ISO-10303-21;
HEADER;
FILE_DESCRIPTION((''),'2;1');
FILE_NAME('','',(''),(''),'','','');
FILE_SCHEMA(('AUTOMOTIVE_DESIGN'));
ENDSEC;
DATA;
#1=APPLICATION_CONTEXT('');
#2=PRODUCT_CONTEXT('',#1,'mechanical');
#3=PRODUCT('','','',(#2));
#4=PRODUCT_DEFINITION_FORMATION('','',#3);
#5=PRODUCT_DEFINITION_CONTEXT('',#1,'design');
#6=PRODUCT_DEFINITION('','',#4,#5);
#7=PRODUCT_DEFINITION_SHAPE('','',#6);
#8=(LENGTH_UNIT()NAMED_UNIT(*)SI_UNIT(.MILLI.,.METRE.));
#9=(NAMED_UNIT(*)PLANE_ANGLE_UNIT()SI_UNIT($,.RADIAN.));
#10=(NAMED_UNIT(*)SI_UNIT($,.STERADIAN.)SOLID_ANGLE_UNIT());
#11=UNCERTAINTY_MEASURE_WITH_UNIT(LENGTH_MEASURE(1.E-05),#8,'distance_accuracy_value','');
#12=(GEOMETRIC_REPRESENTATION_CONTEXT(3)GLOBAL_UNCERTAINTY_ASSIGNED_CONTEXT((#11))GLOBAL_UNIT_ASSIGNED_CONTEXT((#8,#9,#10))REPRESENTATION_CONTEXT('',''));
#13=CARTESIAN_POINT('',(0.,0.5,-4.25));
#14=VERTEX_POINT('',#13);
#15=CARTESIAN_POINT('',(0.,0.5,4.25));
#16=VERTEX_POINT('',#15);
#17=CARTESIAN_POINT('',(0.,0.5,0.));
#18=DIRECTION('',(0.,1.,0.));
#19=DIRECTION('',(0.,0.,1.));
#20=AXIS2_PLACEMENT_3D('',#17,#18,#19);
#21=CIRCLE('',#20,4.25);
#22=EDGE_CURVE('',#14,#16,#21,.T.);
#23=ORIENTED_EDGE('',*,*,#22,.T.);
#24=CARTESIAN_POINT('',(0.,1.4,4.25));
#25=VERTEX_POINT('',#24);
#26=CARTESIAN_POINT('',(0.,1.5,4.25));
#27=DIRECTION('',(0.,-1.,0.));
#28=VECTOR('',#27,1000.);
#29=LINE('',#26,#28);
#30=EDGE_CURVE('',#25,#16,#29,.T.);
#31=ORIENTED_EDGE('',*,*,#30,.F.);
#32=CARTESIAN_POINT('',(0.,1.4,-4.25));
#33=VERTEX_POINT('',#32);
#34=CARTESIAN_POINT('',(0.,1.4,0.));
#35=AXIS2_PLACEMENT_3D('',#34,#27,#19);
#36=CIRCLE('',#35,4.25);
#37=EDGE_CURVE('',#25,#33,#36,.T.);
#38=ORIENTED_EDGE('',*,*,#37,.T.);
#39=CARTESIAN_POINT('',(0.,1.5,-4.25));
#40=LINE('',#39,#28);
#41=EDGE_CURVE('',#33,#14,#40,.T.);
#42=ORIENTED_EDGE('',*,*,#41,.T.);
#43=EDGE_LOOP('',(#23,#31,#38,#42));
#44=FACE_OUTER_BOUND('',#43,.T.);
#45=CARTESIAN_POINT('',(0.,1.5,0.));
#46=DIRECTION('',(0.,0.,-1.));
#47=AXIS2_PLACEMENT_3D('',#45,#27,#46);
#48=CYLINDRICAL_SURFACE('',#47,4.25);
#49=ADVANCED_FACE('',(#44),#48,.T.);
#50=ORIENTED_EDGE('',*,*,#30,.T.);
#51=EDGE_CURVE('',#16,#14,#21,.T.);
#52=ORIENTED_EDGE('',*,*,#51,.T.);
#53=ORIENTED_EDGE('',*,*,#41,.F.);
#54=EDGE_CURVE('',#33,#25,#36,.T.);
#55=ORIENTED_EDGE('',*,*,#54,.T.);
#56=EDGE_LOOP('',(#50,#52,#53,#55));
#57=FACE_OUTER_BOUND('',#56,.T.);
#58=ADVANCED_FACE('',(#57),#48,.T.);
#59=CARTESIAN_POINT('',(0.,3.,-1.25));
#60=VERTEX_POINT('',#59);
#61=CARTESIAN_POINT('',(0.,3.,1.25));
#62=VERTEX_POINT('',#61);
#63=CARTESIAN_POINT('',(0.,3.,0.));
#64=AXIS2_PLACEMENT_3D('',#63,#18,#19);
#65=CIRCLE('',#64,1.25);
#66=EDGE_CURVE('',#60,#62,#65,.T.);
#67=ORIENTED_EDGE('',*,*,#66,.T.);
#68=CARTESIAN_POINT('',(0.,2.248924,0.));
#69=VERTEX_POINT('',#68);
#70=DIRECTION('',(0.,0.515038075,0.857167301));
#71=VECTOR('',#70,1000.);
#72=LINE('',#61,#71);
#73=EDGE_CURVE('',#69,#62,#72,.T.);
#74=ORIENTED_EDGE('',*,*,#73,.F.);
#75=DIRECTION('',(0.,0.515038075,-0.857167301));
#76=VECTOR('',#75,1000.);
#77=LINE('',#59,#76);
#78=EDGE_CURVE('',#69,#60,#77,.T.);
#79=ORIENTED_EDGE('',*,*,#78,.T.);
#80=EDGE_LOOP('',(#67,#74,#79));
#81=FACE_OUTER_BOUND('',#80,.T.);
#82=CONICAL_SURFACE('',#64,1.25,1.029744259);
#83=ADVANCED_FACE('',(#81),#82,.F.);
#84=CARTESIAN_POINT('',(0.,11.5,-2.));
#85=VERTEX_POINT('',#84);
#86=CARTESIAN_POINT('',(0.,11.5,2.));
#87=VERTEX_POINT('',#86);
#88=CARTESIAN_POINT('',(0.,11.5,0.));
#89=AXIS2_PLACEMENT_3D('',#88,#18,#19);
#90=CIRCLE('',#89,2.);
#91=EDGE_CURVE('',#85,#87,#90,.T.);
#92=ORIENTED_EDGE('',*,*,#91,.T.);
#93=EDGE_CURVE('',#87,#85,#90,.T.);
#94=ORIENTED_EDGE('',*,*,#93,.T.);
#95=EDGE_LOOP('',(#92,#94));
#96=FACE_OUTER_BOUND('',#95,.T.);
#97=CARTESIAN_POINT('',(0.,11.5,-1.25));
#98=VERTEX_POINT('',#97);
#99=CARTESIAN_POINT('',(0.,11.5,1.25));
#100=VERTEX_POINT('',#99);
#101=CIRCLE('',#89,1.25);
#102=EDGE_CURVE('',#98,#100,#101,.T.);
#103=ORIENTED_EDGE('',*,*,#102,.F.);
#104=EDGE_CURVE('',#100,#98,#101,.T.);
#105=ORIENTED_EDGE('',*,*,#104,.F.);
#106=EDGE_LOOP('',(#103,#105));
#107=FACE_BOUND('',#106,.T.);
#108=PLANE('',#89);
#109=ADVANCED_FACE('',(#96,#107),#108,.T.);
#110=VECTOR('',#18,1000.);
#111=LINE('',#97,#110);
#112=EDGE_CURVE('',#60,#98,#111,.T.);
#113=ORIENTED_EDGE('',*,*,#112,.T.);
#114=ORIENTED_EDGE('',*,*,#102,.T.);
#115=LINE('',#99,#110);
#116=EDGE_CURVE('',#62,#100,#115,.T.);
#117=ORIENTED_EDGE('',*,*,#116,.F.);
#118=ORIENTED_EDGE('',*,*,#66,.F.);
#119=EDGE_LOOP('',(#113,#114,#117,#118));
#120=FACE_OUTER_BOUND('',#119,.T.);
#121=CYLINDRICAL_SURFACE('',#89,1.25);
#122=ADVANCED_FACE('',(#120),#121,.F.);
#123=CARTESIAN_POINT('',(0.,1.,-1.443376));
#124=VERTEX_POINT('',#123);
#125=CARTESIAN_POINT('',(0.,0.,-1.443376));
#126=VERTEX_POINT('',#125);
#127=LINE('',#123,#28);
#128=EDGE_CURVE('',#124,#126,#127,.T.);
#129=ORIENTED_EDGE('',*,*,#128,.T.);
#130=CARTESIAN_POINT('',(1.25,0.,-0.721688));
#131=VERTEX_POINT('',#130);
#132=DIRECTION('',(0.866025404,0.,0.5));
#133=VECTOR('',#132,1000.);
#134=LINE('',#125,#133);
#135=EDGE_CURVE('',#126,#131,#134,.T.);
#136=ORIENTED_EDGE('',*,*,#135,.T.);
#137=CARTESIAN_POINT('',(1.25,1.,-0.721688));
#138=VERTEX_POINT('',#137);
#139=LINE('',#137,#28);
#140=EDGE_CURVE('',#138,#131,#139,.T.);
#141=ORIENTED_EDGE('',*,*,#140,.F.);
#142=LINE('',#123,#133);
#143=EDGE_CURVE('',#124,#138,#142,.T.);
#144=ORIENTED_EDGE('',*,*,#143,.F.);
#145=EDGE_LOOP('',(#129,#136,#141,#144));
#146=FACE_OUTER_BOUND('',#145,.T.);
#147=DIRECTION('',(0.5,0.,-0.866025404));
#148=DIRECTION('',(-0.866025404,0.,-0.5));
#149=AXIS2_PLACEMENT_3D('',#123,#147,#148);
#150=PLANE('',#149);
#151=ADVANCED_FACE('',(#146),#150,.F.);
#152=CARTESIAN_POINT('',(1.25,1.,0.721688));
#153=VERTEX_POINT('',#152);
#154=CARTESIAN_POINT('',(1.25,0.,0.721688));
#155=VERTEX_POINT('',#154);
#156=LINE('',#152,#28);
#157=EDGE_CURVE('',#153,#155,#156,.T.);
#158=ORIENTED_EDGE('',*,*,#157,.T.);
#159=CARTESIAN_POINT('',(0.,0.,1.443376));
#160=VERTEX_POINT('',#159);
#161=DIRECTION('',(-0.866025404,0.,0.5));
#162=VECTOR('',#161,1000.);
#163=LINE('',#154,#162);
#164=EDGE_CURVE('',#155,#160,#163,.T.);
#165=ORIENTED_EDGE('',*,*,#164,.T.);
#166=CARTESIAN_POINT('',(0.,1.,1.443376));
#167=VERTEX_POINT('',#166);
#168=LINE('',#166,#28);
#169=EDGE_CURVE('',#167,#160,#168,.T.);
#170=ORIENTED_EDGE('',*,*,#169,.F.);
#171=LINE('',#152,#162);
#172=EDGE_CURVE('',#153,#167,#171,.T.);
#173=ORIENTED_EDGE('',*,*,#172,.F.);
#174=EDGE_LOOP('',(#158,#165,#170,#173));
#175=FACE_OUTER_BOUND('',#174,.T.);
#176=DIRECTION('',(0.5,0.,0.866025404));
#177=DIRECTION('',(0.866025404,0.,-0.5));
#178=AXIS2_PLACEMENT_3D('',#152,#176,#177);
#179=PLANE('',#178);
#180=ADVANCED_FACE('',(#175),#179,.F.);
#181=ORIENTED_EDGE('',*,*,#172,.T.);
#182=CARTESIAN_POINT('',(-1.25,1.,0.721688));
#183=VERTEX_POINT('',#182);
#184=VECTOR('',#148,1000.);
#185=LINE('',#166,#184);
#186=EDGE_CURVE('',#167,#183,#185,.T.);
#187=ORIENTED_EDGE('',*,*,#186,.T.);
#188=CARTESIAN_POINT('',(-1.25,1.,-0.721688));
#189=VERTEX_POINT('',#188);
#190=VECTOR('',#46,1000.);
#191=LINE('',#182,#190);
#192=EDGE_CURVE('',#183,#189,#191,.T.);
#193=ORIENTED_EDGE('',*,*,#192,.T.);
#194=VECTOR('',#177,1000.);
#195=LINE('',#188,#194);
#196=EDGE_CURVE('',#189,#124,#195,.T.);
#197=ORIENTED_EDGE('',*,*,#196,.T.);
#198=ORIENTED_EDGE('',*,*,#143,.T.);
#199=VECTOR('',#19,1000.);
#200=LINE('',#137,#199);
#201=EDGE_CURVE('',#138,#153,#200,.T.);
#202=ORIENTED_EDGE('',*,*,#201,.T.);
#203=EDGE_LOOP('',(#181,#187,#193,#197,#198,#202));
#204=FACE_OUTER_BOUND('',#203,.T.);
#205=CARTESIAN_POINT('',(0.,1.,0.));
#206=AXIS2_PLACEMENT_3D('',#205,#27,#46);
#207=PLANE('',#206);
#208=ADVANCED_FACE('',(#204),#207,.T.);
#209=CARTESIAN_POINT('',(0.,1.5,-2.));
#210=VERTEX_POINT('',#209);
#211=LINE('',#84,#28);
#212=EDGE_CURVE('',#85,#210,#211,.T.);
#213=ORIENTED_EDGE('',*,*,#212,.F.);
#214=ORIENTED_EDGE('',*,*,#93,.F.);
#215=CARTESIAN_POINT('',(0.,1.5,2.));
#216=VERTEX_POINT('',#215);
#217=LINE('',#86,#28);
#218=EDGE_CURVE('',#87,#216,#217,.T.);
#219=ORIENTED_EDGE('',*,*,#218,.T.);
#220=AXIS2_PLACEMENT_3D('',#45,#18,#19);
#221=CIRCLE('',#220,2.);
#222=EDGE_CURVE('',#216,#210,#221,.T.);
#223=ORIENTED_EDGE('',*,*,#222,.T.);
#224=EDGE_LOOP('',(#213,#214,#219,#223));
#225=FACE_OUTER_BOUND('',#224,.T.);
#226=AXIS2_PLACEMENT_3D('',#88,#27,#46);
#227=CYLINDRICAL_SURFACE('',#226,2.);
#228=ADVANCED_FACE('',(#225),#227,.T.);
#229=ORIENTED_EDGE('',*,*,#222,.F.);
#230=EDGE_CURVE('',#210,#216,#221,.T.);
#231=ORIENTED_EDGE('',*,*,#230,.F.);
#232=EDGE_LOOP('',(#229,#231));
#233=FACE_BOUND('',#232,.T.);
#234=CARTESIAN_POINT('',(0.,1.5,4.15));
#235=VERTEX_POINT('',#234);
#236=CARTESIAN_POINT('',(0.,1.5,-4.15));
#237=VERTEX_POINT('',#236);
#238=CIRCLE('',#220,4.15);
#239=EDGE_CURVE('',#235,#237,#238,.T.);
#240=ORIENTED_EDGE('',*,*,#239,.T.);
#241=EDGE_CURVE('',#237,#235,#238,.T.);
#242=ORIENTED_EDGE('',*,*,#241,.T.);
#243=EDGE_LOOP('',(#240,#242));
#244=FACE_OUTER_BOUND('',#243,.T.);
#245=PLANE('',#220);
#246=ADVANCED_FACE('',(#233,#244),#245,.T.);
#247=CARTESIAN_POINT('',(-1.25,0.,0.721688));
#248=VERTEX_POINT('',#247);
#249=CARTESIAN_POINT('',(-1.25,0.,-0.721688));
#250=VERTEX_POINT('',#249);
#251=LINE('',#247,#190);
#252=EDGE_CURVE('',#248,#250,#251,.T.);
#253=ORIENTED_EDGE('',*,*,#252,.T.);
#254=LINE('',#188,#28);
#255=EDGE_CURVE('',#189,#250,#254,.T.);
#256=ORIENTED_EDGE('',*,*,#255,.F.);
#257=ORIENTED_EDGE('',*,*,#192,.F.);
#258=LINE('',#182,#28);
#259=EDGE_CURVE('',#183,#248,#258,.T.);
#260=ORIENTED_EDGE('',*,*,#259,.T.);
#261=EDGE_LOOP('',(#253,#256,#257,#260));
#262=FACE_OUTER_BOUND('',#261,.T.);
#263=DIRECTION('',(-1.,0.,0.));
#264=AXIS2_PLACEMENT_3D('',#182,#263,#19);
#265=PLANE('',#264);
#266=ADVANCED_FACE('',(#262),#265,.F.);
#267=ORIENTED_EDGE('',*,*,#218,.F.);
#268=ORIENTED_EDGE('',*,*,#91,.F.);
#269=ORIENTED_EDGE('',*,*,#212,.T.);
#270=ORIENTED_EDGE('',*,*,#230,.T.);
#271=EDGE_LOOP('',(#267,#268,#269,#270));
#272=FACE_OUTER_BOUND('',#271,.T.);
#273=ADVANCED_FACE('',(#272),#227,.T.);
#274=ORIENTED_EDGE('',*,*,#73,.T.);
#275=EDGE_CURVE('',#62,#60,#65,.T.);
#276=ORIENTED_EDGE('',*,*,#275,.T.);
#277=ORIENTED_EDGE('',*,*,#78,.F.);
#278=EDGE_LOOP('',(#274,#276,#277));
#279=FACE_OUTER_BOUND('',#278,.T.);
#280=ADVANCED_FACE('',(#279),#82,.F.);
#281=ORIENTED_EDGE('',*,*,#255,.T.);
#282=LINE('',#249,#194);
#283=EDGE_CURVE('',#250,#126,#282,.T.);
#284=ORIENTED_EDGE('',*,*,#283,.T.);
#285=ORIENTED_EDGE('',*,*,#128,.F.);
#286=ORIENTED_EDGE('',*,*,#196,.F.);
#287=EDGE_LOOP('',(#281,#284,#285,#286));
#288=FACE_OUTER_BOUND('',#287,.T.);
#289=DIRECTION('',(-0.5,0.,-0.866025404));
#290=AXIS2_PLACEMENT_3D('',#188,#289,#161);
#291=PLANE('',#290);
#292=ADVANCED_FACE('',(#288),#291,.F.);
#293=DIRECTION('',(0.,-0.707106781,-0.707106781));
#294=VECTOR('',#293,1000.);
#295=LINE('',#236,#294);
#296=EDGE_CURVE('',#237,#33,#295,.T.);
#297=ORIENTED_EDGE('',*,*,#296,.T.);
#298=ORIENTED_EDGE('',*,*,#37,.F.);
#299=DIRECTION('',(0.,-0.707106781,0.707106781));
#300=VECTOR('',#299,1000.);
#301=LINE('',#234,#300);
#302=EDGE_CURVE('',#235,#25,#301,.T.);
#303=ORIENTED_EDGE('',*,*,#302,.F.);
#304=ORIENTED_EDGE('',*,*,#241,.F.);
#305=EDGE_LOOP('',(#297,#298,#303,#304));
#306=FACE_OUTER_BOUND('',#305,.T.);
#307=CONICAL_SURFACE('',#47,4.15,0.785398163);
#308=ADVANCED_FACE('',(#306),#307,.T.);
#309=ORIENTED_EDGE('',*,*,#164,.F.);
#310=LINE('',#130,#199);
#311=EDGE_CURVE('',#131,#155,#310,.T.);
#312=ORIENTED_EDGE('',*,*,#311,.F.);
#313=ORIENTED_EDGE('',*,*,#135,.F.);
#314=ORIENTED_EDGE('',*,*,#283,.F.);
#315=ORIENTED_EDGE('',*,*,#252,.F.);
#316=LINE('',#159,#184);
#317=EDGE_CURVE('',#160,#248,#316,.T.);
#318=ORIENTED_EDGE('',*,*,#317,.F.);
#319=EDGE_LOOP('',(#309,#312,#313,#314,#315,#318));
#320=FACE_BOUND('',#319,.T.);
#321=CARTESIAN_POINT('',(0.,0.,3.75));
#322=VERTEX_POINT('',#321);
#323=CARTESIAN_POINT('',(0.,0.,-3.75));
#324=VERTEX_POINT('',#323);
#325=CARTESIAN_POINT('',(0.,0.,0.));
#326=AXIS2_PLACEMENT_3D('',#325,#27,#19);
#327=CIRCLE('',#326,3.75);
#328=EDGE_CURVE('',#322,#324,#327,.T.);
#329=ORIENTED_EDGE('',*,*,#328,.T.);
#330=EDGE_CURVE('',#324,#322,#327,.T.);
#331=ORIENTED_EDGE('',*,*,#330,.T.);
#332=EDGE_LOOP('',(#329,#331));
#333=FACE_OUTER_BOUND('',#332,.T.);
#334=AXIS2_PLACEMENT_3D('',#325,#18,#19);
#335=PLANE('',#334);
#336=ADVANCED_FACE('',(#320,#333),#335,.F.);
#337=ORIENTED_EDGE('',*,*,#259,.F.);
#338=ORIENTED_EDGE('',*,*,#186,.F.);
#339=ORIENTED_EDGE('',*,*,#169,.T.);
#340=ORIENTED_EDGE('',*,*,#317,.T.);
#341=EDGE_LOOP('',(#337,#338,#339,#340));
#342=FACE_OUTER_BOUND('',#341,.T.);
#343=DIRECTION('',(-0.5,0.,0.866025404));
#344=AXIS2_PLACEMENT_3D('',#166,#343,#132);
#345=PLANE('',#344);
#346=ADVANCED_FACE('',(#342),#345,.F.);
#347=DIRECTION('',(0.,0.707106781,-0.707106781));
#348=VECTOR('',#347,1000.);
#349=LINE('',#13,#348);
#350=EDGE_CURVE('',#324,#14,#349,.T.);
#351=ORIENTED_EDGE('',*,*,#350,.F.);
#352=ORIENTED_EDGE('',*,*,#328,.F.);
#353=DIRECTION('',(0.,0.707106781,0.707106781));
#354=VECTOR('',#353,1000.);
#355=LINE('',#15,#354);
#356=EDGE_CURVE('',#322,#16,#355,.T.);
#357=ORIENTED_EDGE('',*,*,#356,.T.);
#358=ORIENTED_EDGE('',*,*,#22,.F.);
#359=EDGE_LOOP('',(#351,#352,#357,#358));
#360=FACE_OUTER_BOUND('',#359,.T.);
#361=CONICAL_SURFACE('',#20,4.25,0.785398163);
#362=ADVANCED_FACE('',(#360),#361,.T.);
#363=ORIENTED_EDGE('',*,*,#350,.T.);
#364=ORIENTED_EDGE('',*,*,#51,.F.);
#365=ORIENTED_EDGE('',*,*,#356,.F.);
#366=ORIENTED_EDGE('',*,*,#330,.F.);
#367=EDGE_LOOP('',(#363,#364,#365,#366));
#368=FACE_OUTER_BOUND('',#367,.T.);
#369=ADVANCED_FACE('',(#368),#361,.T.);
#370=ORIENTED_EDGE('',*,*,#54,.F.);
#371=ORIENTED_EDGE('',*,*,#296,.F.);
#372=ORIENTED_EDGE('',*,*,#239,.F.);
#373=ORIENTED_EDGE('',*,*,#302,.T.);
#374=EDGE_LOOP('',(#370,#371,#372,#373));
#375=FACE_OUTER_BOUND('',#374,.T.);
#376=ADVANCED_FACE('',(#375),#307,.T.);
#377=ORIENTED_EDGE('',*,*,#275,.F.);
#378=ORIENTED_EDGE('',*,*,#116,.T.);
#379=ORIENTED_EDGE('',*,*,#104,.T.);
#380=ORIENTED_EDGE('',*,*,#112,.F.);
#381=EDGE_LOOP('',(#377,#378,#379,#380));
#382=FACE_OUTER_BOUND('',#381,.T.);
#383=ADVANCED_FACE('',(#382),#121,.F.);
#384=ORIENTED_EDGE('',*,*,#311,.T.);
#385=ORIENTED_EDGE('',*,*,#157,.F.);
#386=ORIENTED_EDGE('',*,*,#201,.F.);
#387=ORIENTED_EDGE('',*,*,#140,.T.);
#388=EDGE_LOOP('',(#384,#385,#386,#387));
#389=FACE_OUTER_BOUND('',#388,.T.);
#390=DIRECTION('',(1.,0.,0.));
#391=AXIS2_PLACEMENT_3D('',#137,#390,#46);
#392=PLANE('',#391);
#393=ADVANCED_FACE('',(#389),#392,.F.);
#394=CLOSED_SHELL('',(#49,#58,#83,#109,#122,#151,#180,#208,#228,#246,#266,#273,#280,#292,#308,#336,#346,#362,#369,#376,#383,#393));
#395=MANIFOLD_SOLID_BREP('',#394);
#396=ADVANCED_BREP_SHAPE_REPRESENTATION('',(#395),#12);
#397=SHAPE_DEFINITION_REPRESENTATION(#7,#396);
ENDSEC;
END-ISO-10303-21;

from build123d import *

# Parameters (mm, degrees)
SKETCH_1_R             = 4.25
EXTRUDE_1_DEPTH        = 1.5
SKETCH_2_R             = 2
EXTRUDE_2_DEPTH        = 10
HOLE_WIZARD_M3_1_D     = 2.5
HOLE_WIZARD_M3_1_DEPTH = 8.5
HOLE_WIZARD_M3_1_TIP   = 0.751075774
CUT_EXTRUDE_1_DEPTH    = 1
CHAMFER_1_SIZE         = 0.5
CHAMFER_2_SIZE         = 0.1


with BuildPart() as part:
    # 草图1 → 凸台-拉伸1 (new body)
    with BuildSketch(Plane(origin=(0, 0, 0), x_dir=(1, 0, 0), z_dir=(0, 1, 0))):
        with Locations(Location((0, 0, 0), (0, 0, 270))):
            Circle(SKETCH_1_R)
    extrude(amount=EXTRUDE_1_DEPTH)

    # 草图2 → 凸台-拉伸2 (add)
    with BuildSketch(Plane(origin=(0, 1.5, 0), x_dir=(1, 0, 0), z_dir=(0, 1, 0))):
        with Locations(Location((0, 0, 0), (0, 0, 270))):
            Circle(SKETCH_2_R)
    extrude(amount=EXTRUDE_2_DEPTH)

    # M3 螺纹孔1
    with Locations(Plane(origin=(0, 11.5, 0), x_dir=(1, 0, 0), z_dir=(0, 1, 0))):
        with Locations((0, 0)):
            Hole(HOLE_WIZARD_M3_1_D / 2, depth=HOLE_WIZARD_M3_1_DEPTH)
            with Locations((0, 0, -(HOLE_WIZARD_M3_1_DEPTH + HOLE_WIZARD_M3_1_TIP / 2))):  # 118° drill point
                Cone(0, HOLE_WIZARD_M3_1_D / 2, HOLE_WIZARD_M3_1_TIP, mode=Mode.SUBTRACT)

    # 草图7 → 切除-拉伸1 (cut)
    with BuildSketch(Plane.XZ):
        Polygon((0, 1.443375673), (-1.25, 0.721687836), (-1.25, -0.721687836), (0, -1.443375673), (1.25, -0.721687836), (1.25, 0.721687836), align=None)
    extrude(amount=-CUT_EXTRUDE_1_DEPTH, mode=Mode.SUBTRACT)

    # 倒角1
    chamfer_1_edges = [part.edges().sort_by_distance(p)[0] for p in [
        (0, 0, -4.25),
    ]]
    chamfer(chamfer_1_edges, length=CHAMFER_1_SIZE)

    # 倒角2
    chamfer_2_edges = [part.edges().sort_by_distance(p)[0] for p in [
        (0, 1.5, -4.25),
    ]]
    chamfer(chamfer_2_edges, length=CHAMFER_2_SIZE)


solid = part.part
